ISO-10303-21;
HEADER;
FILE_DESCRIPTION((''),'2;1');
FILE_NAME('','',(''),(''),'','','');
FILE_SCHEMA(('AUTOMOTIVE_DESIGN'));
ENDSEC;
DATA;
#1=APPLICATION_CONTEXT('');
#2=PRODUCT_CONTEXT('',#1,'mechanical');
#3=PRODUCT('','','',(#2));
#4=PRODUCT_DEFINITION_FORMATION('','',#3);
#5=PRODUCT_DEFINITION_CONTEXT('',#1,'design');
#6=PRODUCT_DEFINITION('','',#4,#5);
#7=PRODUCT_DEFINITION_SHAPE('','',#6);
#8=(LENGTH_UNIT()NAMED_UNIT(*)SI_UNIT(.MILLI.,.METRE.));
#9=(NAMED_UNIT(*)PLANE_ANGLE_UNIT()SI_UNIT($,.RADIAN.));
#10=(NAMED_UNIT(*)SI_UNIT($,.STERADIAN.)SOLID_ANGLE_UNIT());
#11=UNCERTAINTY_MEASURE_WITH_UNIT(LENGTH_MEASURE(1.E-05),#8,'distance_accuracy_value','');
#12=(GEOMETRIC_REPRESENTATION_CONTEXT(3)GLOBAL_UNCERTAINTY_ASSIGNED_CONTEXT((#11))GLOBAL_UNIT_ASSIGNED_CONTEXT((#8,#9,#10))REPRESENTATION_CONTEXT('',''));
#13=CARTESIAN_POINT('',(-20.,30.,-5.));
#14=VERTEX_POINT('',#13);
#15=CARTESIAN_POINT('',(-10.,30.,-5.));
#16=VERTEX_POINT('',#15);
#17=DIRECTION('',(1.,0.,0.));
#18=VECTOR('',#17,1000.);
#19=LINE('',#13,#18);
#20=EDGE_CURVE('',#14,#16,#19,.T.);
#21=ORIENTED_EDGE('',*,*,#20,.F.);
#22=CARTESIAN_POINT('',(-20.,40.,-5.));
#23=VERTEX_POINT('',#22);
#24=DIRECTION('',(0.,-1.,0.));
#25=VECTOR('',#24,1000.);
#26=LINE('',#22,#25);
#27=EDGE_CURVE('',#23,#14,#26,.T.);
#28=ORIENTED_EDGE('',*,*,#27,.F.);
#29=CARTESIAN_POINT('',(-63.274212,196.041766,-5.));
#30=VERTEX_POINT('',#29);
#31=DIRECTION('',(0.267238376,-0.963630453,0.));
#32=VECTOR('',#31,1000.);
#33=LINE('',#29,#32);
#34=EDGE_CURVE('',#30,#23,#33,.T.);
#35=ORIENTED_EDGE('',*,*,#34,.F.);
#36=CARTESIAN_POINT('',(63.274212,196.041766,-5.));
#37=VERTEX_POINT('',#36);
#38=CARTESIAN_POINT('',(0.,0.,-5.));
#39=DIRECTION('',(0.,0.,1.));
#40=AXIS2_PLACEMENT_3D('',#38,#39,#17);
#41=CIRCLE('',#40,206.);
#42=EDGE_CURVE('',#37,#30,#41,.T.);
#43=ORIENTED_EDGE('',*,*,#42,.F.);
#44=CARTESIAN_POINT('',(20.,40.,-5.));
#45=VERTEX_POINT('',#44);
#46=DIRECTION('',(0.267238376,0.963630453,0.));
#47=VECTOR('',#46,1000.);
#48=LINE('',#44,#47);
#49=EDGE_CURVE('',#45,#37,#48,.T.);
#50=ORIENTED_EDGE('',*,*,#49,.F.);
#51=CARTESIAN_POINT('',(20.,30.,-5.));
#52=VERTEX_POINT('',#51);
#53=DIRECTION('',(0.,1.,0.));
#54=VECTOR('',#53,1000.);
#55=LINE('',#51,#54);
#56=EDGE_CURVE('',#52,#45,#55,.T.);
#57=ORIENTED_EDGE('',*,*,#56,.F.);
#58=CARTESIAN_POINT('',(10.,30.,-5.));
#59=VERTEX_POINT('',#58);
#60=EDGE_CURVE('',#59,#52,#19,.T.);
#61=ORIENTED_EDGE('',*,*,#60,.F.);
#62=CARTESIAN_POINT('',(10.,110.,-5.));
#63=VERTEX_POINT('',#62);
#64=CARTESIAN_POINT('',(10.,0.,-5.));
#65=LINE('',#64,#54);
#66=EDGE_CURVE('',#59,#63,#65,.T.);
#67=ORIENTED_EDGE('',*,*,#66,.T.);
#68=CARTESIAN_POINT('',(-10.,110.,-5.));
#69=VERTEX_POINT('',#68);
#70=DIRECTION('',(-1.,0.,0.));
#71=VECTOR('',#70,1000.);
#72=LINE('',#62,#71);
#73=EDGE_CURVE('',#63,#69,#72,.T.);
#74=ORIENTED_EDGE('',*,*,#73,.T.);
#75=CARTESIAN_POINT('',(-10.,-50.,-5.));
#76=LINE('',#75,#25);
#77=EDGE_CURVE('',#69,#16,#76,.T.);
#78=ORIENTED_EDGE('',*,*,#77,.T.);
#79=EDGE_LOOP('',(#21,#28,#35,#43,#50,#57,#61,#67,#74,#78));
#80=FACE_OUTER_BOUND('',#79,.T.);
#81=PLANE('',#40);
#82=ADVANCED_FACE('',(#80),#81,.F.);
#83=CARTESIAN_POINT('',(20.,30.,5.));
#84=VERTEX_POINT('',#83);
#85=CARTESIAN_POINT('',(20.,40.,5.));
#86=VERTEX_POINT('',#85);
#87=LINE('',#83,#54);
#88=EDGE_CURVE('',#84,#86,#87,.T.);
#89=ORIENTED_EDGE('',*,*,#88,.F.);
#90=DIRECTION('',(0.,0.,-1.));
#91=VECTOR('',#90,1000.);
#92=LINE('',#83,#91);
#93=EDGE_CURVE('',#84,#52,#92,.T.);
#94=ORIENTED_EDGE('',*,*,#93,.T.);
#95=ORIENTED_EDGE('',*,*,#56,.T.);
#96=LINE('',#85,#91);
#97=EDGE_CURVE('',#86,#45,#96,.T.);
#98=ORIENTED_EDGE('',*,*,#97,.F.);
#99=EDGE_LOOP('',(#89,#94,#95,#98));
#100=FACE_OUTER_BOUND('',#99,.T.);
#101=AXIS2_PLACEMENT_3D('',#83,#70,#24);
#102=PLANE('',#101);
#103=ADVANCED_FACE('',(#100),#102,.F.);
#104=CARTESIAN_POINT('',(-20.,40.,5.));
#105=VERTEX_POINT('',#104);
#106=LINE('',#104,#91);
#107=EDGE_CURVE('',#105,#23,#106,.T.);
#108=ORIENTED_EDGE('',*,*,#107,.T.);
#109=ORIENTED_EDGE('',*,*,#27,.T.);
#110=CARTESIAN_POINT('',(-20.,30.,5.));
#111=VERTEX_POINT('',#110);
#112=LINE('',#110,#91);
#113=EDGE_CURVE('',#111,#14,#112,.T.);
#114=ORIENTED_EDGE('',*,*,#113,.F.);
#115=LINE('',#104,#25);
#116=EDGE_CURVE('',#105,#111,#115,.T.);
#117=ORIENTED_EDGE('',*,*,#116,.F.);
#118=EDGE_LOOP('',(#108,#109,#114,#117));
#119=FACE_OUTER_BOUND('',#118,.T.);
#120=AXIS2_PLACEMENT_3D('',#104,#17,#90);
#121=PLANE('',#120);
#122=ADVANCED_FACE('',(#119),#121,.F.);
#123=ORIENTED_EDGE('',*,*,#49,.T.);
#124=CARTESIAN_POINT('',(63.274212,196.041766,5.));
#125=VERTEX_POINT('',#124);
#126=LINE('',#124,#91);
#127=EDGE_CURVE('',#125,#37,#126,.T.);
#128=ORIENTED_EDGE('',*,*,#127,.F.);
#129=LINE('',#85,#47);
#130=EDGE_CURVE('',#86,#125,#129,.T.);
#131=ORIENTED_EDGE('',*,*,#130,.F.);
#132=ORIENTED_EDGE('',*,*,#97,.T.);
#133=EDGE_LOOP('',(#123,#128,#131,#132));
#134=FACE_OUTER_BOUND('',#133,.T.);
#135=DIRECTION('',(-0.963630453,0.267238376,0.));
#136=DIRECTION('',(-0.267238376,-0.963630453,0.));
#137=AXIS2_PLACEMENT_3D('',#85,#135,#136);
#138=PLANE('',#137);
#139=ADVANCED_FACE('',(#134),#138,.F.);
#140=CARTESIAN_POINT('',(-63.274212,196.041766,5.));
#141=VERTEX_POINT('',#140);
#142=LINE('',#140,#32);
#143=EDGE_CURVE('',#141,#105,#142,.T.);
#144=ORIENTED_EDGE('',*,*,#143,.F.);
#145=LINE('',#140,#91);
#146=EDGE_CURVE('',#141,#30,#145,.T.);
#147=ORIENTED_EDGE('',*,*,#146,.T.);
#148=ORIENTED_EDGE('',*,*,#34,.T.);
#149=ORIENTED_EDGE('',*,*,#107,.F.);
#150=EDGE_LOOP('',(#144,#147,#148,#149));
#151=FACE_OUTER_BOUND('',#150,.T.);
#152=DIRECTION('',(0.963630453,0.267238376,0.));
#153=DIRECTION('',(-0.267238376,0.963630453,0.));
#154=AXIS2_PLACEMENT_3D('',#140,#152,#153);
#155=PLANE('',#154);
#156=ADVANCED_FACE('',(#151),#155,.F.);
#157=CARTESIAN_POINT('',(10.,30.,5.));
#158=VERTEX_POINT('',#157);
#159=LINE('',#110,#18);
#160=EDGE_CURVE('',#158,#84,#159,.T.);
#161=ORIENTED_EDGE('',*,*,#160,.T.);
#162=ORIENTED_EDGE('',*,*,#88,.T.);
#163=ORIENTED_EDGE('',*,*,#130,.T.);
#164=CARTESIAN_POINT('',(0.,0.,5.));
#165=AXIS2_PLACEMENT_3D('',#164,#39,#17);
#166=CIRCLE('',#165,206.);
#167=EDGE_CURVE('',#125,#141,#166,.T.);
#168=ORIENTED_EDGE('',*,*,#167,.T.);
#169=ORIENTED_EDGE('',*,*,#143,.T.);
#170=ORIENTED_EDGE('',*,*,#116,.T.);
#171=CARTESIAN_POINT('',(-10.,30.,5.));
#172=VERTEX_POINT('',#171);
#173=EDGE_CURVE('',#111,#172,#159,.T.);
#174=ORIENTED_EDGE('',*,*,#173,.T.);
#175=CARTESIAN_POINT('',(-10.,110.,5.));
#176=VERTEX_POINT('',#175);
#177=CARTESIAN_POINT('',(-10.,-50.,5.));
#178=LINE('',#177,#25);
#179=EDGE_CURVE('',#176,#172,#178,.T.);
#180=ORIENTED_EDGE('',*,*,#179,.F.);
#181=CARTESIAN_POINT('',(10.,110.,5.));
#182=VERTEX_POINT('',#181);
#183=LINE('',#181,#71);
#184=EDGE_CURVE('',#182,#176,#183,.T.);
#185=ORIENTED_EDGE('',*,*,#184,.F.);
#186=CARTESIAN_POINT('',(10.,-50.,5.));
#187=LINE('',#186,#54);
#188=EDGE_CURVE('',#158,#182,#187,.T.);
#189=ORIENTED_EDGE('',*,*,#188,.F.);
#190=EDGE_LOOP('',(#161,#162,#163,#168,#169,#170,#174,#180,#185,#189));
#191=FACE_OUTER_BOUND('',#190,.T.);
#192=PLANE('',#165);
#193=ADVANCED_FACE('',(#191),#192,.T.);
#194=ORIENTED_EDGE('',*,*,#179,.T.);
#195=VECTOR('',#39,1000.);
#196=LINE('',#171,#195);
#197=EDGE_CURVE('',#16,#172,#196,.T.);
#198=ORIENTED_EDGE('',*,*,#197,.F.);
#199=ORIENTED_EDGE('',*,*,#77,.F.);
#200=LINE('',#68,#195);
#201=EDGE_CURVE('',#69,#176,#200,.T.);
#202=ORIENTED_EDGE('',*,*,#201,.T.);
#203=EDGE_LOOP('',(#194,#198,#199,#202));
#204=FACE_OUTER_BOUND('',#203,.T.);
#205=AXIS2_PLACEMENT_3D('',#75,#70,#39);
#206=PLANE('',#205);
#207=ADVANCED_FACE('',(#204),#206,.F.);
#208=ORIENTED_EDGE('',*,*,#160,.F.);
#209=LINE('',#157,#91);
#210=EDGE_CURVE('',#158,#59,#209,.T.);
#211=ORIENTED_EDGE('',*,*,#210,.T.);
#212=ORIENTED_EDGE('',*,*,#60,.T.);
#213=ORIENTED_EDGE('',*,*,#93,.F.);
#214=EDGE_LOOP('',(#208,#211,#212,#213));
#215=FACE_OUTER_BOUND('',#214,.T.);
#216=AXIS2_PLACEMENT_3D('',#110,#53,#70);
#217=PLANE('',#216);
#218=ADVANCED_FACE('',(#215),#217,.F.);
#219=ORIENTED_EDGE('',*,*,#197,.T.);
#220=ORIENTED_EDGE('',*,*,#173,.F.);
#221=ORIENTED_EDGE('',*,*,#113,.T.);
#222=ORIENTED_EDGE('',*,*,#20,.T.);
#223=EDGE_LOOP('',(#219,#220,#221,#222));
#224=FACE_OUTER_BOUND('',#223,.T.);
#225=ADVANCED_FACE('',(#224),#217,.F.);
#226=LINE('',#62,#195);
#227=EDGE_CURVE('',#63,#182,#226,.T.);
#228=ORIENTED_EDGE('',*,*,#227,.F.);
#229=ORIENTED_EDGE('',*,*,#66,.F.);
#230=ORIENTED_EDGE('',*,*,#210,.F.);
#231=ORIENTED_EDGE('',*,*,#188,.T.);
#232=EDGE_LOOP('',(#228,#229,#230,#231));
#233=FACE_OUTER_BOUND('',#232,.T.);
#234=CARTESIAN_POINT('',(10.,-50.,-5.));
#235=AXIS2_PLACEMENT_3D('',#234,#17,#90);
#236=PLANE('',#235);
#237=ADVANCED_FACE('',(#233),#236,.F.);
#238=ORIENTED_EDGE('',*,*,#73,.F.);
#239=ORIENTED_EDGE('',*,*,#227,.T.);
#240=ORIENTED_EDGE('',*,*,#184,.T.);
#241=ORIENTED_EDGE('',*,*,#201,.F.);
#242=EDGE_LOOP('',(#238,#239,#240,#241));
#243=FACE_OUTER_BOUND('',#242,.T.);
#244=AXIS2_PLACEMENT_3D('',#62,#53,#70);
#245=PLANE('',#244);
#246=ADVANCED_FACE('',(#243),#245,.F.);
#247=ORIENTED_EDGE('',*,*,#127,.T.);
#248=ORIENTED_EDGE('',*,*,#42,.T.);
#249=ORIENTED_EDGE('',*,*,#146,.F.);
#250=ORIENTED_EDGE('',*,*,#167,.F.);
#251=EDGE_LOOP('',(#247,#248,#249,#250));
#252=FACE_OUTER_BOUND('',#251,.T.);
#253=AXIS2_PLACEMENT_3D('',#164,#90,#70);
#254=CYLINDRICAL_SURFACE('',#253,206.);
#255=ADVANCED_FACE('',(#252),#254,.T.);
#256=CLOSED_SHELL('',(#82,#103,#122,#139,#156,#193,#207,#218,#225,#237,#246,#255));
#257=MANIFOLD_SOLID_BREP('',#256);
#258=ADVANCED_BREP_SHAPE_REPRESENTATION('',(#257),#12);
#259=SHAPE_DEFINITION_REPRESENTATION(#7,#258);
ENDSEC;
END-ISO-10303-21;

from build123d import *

# Parameters (mm, degrees)
BOSS_EXTRUDE1_DEPTH = 5
SKETCH2_W           = 20
SKETCH2_H           = 160
CUT_EXTRUDE1_DEPTH  = 10


with BuildPart() as part:
    # Sketch1 → Boss-Extrude1 (new, symmetric)
    with BuildSketch(Plane.XY):
        with BuildLine():
            Line((-63.274211694, 196.041766301), (-20, 40))
            Line((-20, 40), (-20, 30))
            Line((-20, 30), (20, 30))
            Line((20, 30), (20, 40))
            Line((20, 40), (63.274211694, 196.041766301))
            ThreePointArc((63.274211694, 196.041766301), (0, 206), (-63.274211694, 196.041766301))
        make_face()
    extrude(amount=BOSS_EXTRUDE1_DEPTH, both=True)

    # Sketch2 → Cut-Extrude1 (cut)
    with BuildSketch(Plane.XY.offset(5)):
        with Locations((0, 30)):
            Rectangle(SKETCH2_W, SKETCH2_H)
    extrude(amount=-CUT_EXTRUDE1_DEPTH, mode=Mode.SUBTRACT)


solid = part.part
